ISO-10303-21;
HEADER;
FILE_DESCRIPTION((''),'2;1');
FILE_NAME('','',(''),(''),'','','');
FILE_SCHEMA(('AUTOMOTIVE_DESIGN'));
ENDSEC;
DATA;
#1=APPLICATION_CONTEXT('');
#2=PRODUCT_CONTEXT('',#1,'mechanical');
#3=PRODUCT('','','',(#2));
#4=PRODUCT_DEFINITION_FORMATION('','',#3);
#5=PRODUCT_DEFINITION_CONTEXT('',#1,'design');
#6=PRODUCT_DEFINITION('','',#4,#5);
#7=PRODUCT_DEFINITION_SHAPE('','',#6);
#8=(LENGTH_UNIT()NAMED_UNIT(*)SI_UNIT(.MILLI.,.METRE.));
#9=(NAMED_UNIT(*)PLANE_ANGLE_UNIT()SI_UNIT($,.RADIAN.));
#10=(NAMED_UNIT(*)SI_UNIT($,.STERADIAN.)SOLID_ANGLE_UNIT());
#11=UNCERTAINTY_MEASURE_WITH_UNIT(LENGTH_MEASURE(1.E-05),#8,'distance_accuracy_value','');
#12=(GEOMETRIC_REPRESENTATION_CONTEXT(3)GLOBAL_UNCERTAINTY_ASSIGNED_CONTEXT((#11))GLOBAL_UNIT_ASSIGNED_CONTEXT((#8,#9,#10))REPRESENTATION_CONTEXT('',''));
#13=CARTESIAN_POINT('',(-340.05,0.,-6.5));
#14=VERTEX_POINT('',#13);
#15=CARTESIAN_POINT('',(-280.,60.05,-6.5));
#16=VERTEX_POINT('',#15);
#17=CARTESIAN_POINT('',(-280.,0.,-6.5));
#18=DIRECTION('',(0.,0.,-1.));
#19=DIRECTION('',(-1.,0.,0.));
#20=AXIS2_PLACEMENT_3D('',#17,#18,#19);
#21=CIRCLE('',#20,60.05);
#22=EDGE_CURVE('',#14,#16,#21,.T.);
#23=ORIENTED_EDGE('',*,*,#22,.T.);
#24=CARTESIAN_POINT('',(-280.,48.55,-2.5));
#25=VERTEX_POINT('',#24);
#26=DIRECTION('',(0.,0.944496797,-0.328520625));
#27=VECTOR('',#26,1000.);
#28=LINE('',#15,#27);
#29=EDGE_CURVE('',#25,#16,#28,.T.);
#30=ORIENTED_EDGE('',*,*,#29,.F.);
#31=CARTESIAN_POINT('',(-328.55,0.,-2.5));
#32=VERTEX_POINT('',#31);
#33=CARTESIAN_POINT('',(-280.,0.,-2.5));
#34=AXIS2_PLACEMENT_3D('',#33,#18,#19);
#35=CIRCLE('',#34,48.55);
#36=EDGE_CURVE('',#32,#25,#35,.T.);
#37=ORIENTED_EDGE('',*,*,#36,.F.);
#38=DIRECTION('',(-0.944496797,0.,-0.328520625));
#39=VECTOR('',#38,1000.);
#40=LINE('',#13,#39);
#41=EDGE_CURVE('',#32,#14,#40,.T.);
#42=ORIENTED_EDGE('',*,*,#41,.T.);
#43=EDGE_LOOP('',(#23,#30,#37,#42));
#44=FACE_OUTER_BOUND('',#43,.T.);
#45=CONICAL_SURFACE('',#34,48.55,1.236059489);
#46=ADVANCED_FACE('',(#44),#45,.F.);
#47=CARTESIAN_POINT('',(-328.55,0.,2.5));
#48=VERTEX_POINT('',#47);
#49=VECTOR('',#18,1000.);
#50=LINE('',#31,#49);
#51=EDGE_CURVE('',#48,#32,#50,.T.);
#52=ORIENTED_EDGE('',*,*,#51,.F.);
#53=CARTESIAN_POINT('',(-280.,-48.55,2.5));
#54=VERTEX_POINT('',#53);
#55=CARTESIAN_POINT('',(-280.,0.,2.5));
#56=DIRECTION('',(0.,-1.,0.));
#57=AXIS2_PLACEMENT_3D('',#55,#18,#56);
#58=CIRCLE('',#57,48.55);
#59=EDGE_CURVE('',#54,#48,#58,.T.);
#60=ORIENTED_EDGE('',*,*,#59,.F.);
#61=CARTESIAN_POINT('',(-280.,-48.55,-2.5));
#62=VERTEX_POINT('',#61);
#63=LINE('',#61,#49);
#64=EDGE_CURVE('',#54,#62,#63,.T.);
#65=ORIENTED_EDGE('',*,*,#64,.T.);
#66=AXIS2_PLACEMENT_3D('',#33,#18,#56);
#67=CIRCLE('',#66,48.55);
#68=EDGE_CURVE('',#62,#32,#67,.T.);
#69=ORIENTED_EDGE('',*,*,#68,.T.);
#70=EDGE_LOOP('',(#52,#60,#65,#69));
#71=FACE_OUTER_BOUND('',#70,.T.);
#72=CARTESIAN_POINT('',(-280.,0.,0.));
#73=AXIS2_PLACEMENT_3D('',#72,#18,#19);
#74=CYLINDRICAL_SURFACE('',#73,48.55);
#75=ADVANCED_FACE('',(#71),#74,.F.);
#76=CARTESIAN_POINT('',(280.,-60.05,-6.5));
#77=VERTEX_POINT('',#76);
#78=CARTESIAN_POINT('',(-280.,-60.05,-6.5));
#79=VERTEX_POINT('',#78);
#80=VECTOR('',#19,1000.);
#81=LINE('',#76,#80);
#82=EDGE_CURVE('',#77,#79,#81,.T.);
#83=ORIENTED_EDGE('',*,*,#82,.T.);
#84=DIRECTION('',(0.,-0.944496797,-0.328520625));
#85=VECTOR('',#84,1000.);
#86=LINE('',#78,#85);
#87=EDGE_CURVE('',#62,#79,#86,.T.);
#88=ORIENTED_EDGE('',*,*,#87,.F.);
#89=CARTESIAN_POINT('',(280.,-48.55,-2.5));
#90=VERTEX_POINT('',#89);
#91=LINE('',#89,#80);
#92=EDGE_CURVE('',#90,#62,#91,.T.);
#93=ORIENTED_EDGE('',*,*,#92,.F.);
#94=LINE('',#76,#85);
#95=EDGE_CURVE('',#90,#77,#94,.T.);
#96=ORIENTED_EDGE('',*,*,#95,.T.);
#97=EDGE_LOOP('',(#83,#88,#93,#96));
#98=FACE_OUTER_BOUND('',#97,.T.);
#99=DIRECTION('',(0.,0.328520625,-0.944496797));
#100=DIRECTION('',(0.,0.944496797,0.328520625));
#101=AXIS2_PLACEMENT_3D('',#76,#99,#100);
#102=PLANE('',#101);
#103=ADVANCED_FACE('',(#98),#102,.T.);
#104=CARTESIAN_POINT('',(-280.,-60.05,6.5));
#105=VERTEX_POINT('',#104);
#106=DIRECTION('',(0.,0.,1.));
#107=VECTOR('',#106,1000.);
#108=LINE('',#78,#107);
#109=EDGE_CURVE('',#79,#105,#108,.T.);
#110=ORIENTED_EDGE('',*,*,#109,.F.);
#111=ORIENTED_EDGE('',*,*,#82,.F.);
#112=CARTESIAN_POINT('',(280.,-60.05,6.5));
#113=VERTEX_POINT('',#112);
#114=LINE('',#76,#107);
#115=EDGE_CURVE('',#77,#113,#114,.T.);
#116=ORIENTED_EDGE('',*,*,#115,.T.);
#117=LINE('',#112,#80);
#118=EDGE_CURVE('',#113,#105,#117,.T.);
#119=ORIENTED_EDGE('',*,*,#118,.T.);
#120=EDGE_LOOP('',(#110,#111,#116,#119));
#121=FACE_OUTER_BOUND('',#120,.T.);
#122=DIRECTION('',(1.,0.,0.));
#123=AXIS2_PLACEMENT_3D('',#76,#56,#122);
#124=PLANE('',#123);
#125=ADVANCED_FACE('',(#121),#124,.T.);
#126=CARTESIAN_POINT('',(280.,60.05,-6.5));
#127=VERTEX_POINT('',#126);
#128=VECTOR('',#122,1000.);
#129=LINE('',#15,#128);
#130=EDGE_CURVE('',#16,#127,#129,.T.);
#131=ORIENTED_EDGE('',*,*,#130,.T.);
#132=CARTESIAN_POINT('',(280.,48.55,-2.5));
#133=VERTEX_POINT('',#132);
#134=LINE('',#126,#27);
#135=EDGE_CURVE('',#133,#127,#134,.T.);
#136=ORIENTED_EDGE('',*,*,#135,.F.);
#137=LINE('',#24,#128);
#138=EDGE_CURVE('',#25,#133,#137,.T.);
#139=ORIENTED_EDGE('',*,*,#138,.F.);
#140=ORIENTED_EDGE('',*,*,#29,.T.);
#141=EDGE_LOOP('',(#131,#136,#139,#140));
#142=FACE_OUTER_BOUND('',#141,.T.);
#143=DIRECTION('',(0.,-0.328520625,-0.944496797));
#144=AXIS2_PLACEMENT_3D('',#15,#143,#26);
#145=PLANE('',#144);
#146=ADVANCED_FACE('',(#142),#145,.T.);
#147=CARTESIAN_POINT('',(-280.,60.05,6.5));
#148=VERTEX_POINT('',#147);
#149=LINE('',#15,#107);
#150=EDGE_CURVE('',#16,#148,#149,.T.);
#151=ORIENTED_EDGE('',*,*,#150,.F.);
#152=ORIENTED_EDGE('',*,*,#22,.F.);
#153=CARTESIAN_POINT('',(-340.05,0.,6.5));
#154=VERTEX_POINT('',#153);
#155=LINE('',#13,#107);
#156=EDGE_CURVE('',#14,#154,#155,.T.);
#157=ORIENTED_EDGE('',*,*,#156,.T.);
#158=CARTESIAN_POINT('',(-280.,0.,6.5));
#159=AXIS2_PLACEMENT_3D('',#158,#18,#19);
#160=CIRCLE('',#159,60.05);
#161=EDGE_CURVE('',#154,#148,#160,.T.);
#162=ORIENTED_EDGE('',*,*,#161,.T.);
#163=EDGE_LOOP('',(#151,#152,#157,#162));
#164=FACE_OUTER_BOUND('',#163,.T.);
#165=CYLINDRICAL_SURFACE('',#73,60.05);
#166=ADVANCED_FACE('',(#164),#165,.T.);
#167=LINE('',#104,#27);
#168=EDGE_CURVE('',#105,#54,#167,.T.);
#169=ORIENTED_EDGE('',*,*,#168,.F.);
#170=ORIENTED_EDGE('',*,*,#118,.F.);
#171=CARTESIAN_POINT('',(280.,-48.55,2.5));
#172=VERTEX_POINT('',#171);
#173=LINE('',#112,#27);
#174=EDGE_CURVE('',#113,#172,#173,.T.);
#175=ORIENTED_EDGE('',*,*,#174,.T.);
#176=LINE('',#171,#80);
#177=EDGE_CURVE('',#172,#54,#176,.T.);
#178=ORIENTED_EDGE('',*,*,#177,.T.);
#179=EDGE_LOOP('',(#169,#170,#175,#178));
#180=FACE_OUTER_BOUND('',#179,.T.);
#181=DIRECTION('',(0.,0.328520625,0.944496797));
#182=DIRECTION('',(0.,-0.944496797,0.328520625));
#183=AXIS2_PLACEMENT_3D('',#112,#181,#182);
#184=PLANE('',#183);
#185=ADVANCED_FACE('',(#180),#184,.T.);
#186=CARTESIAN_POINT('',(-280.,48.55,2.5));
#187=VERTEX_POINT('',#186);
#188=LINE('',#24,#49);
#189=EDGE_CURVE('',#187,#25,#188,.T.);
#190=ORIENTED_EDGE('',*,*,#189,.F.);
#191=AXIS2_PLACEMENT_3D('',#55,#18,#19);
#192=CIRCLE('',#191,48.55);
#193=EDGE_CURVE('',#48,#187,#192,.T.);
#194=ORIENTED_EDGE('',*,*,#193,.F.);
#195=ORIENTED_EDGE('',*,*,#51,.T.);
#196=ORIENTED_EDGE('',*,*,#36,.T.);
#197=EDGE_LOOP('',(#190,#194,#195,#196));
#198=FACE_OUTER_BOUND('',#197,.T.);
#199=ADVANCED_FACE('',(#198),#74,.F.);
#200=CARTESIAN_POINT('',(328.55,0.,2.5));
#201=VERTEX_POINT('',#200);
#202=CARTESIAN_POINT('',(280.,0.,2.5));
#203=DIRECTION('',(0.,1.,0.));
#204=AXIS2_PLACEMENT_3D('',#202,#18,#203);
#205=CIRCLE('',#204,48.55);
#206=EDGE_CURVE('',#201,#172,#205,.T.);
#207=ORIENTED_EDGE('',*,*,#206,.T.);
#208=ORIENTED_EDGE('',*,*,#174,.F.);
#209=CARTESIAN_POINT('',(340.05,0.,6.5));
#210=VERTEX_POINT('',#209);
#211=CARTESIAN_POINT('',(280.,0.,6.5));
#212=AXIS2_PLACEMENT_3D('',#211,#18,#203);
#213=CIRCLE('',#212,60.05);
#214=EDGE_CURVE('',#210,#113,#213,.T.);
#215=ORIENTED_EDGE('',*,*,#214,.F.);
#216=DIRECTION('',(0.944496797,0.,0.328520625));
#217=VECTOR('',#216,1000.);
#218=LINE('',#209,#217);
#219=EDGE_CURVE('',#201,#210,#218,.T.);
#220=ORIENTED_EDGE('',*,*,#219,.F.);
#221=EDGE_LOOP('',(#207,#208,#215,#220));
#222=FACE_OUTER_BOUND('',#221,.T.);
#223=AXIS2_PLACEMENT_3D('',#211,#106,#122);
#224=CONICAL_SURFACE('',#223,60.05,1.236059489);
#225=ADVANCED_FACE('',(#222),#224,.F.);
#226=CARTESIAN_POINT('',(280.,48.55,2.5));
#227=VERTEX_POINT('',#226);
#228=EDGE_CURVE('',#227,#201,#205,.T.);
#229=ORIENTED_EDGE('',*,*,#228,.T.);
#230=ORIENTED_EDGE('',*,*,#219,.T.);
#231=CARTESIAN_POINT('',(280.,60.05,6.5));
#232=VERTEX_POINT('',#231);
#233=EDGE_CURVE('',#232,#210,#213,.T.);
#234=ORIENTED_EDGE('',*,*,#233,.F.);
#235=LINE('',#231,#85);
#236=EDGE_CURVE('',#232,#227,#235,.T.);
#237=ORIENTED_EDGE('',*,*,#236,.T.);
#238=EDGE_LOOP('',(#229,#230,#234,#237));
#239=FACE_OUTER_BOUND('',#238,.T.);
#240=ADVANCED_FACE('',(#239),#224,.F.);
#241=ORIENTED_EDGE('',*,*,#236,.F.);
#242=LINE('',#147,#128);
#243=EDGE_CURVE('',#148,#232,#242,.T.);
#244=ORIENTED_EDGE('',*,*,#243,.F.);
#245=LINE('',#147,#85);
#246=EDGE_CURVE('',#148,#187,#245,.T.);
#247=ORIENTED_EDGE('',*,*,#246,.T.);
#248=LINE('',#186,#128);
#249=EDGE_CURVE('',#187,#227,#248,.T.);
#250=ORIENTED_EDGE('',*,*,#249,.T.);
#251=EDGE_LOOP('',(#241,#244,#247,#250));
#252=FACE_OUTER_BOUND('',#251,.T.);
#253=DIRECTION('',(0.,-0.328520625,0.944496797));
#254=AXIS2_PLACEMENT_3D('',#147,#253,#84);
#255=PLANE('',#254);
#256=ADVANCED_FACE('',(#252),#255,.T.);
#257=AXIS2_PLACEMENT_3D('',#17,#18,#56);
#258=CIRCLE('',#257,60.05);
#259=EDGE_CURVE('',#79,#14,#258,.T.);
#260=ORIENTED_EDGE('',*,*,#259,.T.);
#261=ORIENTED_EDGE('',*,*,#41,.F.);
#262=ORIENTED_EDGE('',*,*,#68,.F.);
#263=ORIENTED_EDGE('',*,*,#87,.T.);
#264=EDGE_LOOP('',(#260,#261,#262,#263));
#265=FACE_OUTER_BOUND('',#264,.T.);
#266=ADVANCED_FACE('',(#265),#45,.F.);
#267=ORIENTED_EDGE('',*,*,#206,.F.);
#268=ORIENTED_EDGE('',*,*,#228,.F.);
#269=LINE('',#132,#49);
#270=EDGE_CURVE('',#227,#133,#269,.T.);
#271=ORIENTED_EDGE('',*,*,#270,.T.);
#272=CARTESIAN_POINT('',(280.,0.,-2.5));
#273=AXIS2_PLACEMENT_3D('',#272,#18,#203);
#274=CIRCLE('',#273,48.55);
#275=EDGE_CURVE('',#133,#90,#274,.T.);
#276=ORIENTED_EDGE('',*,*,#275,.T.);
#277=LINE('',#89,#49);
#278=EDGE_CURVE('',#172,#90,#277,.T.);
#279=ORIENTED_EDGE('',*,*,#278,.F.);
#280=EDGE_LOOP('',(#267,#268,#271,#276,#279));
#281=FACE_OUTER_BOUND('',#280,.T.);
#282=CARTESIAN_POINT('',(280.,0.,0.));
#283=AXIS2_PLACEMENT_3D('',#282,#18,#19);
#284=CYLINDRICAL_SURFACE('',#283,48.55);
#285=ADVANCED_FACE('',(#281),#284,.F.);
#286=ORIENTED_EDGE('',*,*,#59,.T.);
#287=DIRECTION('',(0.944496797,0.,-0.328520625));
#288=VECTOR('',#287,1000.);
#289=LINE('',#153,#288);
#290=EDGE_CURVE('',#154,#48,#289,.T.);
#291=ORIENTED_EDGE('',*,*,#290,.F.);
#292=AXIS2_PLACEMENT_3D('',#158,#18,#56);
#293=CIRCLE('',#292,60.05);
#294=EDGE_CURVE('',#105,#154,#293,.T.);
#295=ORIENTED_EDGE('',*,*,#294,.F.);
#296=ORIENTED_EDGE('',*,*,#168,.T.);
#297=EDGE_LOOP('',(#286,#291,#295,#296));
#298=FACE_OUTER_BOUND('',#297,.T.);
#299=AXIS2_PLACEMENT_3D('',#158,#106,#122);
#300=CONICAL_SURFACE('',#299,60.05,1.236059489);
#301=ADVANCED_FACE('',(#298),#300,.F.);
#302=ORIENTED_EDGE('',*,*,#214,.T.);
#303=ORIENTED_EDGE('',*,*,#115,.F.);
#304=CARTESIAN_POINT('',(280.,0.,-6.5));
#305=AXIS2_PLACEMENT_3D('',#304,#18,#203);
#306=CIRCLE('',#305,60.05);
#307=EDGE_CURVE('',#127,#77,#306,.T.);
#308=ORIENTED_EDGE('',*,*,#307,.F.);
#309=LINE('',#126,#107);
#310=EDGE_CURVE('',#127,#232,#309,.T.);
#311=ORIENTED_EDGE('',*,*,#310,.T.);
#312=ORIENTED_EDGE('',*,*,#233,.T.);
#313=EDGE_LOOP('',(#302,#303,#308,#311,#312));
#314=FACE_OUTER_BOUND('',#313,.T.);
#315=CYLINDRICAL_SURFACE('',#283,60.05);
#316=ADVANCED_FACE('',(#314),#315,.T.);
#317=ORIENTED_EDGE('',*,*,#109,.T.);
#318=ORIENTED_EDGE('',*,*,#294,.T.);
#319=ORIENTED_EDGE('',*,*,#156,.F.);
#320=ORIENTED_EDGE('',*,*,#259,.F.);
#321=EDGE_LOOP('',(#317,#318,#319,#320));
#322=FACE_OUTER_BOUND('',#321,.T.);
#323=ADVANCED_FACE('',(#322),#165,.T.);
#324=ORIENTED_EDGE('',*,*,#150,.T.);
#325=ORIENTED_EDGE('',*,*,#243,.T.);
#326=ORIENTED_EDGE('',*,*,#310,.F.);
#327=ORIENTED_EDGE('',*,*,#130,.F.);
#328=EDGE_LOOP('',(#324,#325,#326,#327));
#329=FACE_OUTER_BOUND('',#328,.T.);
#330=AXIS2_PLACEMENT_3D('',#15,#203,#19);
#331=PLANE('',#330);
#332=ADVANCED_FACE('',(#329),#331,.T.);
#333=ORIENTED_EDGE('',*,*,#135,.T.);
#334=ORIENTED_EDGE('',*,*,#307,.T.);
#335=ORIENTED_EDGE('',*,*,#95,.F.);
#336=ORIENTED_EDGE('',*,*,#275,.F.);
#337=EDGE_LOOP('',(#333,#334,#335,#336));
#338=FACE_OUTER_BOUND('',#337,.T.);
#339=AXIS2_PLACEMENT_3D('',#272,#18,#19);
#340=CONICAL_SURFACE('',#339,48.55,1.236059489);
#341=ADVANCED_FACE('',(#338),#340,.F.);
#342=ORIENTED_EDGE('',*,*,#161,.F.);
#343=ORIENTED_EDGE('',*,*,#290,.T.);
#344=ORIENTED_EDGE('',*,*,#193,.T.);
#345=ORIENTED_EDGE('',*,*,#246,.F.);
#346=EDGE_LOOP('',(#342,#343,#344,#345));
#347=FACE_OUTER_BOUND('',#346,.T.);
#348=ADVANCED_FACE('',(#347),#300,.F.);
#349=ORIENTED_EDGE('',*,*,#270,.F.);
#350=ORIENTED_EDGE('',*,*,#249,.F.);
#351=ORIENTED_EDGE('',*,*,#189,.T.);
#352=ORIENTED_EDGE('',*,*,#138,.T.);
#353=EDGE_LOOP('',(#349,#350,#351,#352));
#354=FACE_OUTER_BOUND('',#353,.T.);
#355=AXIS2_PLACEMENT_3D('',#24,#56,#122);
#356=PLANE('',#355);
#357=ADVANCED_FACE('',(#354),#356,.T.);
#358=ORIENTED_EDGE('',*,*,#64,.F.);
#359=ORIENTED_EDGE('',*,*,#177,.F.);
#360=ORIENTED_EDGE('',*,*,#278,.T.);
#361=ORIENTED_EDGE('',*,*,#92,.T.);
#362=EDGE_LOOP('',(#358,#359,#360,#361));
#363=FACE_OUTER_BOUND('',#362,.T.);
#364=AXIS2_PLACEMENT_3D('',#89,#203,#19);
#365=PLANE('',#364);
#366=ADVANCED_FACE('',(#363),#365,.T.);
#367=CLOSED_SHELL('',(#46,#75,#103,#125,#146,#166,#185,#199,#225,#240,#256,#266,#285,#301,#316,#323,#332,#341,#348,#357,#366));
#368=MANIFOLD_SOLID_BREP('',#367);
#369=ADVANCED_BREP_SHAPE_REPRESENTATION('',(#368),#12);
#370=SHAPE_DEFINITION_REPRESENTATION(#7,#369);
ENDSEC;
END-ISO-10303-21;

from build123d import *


with BuildPart() as part:
    # Sweep1: sweep along a path in Sketch1
    with BuildLine(Plane.XY) as sweep1_path:
        Line((-280, 48.55), (280, 48.55))
        ThreePointArc((280, 48.55), (328.55, 0), (280, -48.55))
        Line((280, -48.55), (-280, -48.55))
        ThreePointArc((-280, -48.55), (-328.55, 0), (-280, 48.55))
    # Sketch2 → Sweep1 (sweep)
    with BuildSketch(Plane(origin=(0, 0, 0), x_dir=(1, 0, 0), z_dir=(0, 1, 0))):
        Polygon((-328.55, 2.5), (-328.55, -2.5), (-340.05, -6.5), (-340.05, 6.5), align=None)
    sweep(path=sweep1_path.line)


solid = part.part
